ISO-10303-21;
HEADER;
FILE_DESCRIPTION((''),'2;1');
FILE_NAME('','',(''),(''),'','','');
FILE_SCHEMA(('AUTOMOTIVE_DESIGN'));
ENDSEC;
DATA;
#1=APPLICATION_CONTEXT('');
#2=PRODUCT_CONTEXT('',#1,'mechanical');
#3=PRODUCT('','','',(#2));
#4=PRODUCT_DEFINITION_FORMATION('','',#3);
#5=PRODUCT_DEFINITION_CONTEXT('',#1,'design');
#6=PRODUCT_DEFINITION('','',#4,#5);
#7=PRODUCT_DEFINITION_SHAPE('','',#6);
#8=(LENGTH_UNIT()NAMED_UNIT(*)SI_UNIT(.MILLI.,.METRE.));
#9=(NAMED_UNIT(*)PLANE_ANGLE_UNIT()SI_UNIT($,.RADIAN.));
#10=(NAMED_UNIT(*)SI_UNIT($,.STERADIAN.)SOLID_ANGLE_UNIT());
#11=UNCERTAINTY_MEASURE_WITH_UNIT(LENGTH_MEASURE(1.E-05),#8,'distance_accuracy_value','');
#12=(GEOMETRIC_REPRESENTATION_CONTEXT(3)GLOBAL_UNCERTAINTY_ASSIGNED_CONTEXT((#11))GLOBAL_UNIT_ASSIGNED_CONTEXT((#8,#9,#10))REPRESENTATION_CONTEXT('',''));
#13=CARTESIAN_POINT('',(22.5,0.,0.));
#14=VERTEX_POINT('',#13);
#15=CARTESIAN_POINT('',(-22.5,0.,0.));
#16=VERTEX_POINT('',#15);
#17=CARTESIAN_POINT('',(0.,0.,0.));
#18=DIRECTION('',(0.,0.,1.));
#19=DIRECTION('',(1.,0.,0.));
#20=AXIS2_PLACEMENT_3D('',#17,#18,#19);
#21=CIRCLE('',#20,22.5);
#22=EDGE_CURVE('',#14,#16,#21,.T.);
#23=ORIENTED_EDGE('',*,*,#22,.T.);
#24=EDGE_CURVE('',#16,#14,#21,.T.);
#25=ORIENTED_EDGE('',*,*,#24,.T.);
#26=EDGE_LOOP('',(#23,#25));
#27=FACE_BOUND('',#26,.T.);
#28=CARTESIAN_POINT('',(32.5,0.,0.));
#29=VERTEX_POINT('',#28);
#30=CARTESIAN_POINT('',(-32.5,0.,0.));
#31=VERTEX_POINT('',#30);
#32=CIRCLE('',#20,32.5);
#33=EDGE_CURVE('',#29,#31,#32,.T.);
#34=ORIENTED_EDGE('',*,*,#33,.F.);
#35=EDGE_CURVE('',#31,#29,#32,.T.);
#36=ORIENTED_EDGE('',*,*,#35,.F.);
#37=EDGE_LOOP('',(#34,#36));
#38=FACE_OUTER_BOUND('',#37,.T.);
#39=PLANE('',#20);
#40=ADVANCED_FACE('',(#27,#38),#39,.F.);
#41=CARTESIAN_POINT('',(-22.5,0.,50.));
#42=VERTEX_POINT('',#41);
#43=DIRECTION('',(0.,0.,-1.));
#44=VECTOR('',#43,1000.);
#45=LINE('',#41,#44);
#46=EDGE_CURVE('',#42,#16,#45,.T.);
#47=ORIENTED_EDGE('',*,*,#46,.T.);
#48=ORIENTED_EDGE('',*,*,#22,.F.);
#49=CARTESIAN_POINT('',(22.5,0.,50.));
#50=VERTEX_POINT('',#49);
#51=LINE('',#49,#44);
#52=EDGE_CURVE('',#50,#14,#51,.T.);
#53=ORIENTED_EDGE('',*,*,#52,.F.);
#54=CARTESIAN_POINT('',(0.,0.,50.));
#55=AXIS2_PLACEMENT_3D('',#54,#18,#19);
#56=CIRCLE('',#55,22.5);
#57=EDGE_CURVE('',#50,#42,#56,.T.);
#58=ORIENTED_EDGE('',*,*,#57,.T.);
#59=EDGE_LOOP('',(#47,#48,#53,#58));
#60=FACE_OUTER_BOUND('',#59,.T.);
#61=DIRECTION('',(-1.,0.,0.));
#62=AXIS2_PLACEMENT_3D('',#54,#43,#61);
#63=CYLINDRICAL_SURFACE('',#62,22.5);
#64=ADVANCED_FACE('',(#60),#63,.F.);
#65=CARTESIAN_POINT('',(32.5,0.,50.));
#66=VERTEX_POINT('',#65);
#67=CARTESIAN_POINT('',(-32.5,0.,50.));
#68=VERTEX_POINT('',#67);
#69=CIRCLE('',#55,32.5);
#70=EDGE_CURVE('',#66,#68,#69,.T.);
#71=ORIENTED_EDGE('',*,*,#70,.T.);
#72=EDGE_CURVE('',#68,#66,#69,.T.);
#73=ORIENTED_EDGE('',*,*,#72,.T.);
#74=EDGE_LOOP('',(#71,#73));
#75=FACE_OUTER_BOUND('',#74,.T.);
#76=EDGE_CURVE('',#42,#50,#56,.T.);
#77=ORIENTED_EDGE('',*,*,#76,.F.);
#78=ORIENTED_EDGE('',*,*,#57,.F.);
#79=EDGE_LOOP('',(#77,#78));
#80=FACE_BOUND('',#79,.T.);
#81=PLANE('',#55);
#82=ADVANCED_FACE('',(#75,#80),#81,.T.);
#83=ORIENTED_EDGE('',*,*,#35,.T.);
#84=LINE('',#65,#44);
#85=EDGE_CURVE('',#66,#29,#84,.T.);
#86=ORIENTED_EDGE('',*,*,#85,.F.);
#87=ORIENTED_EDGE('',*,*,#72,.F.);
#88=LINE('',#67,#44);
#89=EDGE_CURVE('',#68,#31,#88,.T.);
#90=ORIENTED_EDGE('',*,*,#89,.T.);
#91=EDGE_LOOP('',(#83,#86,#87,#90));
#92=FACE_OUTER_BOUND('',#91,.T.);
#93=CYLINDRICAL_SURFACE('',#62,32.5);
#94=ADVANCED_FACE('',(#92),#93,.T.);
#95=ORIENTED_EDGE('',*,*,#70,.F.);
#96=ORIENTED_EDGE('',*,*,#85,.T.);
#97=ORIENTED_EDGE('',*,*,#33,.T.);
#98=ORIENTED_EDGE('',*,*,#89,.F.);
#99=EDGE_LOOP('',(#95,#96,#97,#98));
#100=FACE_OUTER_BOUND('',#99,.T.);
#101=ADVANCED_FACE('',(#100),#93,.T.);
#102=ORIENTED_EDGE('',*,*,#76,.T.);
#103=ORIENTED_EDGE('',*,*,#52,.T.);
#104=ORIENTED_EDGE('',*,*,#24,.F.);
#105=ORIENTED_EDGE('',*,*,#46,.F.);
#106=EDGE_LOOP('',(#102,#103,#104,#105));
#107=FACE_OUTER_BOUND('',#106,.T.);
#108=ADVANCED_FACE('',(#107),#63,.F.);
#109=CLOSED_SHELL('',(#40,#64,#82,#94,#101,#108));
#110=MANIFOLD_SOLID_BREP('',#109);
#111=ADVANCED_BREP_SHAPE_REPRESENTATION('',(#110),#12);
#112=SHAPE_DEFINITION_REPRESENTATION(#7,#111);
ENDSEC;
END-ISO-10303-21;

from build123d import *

# Parameters (mm, degrees)
SKETCH_1_R      = 32.5
SKETCH_1_R_2    = 22.5
EXTRUDE_1_DEPTH = 50


with BuildPart() as part:
    # 草图1 → 凸台-拉伸1 (new body)
    with BuildSketch(Plane.XY):
        Circle(SKETCH_1_R)
        Circle(SKETCH_1_R_2, mode=Mode.SUBTRACT)
    extrude(amount=EXTRUDE_1_DEPTH)


solid = part.part
